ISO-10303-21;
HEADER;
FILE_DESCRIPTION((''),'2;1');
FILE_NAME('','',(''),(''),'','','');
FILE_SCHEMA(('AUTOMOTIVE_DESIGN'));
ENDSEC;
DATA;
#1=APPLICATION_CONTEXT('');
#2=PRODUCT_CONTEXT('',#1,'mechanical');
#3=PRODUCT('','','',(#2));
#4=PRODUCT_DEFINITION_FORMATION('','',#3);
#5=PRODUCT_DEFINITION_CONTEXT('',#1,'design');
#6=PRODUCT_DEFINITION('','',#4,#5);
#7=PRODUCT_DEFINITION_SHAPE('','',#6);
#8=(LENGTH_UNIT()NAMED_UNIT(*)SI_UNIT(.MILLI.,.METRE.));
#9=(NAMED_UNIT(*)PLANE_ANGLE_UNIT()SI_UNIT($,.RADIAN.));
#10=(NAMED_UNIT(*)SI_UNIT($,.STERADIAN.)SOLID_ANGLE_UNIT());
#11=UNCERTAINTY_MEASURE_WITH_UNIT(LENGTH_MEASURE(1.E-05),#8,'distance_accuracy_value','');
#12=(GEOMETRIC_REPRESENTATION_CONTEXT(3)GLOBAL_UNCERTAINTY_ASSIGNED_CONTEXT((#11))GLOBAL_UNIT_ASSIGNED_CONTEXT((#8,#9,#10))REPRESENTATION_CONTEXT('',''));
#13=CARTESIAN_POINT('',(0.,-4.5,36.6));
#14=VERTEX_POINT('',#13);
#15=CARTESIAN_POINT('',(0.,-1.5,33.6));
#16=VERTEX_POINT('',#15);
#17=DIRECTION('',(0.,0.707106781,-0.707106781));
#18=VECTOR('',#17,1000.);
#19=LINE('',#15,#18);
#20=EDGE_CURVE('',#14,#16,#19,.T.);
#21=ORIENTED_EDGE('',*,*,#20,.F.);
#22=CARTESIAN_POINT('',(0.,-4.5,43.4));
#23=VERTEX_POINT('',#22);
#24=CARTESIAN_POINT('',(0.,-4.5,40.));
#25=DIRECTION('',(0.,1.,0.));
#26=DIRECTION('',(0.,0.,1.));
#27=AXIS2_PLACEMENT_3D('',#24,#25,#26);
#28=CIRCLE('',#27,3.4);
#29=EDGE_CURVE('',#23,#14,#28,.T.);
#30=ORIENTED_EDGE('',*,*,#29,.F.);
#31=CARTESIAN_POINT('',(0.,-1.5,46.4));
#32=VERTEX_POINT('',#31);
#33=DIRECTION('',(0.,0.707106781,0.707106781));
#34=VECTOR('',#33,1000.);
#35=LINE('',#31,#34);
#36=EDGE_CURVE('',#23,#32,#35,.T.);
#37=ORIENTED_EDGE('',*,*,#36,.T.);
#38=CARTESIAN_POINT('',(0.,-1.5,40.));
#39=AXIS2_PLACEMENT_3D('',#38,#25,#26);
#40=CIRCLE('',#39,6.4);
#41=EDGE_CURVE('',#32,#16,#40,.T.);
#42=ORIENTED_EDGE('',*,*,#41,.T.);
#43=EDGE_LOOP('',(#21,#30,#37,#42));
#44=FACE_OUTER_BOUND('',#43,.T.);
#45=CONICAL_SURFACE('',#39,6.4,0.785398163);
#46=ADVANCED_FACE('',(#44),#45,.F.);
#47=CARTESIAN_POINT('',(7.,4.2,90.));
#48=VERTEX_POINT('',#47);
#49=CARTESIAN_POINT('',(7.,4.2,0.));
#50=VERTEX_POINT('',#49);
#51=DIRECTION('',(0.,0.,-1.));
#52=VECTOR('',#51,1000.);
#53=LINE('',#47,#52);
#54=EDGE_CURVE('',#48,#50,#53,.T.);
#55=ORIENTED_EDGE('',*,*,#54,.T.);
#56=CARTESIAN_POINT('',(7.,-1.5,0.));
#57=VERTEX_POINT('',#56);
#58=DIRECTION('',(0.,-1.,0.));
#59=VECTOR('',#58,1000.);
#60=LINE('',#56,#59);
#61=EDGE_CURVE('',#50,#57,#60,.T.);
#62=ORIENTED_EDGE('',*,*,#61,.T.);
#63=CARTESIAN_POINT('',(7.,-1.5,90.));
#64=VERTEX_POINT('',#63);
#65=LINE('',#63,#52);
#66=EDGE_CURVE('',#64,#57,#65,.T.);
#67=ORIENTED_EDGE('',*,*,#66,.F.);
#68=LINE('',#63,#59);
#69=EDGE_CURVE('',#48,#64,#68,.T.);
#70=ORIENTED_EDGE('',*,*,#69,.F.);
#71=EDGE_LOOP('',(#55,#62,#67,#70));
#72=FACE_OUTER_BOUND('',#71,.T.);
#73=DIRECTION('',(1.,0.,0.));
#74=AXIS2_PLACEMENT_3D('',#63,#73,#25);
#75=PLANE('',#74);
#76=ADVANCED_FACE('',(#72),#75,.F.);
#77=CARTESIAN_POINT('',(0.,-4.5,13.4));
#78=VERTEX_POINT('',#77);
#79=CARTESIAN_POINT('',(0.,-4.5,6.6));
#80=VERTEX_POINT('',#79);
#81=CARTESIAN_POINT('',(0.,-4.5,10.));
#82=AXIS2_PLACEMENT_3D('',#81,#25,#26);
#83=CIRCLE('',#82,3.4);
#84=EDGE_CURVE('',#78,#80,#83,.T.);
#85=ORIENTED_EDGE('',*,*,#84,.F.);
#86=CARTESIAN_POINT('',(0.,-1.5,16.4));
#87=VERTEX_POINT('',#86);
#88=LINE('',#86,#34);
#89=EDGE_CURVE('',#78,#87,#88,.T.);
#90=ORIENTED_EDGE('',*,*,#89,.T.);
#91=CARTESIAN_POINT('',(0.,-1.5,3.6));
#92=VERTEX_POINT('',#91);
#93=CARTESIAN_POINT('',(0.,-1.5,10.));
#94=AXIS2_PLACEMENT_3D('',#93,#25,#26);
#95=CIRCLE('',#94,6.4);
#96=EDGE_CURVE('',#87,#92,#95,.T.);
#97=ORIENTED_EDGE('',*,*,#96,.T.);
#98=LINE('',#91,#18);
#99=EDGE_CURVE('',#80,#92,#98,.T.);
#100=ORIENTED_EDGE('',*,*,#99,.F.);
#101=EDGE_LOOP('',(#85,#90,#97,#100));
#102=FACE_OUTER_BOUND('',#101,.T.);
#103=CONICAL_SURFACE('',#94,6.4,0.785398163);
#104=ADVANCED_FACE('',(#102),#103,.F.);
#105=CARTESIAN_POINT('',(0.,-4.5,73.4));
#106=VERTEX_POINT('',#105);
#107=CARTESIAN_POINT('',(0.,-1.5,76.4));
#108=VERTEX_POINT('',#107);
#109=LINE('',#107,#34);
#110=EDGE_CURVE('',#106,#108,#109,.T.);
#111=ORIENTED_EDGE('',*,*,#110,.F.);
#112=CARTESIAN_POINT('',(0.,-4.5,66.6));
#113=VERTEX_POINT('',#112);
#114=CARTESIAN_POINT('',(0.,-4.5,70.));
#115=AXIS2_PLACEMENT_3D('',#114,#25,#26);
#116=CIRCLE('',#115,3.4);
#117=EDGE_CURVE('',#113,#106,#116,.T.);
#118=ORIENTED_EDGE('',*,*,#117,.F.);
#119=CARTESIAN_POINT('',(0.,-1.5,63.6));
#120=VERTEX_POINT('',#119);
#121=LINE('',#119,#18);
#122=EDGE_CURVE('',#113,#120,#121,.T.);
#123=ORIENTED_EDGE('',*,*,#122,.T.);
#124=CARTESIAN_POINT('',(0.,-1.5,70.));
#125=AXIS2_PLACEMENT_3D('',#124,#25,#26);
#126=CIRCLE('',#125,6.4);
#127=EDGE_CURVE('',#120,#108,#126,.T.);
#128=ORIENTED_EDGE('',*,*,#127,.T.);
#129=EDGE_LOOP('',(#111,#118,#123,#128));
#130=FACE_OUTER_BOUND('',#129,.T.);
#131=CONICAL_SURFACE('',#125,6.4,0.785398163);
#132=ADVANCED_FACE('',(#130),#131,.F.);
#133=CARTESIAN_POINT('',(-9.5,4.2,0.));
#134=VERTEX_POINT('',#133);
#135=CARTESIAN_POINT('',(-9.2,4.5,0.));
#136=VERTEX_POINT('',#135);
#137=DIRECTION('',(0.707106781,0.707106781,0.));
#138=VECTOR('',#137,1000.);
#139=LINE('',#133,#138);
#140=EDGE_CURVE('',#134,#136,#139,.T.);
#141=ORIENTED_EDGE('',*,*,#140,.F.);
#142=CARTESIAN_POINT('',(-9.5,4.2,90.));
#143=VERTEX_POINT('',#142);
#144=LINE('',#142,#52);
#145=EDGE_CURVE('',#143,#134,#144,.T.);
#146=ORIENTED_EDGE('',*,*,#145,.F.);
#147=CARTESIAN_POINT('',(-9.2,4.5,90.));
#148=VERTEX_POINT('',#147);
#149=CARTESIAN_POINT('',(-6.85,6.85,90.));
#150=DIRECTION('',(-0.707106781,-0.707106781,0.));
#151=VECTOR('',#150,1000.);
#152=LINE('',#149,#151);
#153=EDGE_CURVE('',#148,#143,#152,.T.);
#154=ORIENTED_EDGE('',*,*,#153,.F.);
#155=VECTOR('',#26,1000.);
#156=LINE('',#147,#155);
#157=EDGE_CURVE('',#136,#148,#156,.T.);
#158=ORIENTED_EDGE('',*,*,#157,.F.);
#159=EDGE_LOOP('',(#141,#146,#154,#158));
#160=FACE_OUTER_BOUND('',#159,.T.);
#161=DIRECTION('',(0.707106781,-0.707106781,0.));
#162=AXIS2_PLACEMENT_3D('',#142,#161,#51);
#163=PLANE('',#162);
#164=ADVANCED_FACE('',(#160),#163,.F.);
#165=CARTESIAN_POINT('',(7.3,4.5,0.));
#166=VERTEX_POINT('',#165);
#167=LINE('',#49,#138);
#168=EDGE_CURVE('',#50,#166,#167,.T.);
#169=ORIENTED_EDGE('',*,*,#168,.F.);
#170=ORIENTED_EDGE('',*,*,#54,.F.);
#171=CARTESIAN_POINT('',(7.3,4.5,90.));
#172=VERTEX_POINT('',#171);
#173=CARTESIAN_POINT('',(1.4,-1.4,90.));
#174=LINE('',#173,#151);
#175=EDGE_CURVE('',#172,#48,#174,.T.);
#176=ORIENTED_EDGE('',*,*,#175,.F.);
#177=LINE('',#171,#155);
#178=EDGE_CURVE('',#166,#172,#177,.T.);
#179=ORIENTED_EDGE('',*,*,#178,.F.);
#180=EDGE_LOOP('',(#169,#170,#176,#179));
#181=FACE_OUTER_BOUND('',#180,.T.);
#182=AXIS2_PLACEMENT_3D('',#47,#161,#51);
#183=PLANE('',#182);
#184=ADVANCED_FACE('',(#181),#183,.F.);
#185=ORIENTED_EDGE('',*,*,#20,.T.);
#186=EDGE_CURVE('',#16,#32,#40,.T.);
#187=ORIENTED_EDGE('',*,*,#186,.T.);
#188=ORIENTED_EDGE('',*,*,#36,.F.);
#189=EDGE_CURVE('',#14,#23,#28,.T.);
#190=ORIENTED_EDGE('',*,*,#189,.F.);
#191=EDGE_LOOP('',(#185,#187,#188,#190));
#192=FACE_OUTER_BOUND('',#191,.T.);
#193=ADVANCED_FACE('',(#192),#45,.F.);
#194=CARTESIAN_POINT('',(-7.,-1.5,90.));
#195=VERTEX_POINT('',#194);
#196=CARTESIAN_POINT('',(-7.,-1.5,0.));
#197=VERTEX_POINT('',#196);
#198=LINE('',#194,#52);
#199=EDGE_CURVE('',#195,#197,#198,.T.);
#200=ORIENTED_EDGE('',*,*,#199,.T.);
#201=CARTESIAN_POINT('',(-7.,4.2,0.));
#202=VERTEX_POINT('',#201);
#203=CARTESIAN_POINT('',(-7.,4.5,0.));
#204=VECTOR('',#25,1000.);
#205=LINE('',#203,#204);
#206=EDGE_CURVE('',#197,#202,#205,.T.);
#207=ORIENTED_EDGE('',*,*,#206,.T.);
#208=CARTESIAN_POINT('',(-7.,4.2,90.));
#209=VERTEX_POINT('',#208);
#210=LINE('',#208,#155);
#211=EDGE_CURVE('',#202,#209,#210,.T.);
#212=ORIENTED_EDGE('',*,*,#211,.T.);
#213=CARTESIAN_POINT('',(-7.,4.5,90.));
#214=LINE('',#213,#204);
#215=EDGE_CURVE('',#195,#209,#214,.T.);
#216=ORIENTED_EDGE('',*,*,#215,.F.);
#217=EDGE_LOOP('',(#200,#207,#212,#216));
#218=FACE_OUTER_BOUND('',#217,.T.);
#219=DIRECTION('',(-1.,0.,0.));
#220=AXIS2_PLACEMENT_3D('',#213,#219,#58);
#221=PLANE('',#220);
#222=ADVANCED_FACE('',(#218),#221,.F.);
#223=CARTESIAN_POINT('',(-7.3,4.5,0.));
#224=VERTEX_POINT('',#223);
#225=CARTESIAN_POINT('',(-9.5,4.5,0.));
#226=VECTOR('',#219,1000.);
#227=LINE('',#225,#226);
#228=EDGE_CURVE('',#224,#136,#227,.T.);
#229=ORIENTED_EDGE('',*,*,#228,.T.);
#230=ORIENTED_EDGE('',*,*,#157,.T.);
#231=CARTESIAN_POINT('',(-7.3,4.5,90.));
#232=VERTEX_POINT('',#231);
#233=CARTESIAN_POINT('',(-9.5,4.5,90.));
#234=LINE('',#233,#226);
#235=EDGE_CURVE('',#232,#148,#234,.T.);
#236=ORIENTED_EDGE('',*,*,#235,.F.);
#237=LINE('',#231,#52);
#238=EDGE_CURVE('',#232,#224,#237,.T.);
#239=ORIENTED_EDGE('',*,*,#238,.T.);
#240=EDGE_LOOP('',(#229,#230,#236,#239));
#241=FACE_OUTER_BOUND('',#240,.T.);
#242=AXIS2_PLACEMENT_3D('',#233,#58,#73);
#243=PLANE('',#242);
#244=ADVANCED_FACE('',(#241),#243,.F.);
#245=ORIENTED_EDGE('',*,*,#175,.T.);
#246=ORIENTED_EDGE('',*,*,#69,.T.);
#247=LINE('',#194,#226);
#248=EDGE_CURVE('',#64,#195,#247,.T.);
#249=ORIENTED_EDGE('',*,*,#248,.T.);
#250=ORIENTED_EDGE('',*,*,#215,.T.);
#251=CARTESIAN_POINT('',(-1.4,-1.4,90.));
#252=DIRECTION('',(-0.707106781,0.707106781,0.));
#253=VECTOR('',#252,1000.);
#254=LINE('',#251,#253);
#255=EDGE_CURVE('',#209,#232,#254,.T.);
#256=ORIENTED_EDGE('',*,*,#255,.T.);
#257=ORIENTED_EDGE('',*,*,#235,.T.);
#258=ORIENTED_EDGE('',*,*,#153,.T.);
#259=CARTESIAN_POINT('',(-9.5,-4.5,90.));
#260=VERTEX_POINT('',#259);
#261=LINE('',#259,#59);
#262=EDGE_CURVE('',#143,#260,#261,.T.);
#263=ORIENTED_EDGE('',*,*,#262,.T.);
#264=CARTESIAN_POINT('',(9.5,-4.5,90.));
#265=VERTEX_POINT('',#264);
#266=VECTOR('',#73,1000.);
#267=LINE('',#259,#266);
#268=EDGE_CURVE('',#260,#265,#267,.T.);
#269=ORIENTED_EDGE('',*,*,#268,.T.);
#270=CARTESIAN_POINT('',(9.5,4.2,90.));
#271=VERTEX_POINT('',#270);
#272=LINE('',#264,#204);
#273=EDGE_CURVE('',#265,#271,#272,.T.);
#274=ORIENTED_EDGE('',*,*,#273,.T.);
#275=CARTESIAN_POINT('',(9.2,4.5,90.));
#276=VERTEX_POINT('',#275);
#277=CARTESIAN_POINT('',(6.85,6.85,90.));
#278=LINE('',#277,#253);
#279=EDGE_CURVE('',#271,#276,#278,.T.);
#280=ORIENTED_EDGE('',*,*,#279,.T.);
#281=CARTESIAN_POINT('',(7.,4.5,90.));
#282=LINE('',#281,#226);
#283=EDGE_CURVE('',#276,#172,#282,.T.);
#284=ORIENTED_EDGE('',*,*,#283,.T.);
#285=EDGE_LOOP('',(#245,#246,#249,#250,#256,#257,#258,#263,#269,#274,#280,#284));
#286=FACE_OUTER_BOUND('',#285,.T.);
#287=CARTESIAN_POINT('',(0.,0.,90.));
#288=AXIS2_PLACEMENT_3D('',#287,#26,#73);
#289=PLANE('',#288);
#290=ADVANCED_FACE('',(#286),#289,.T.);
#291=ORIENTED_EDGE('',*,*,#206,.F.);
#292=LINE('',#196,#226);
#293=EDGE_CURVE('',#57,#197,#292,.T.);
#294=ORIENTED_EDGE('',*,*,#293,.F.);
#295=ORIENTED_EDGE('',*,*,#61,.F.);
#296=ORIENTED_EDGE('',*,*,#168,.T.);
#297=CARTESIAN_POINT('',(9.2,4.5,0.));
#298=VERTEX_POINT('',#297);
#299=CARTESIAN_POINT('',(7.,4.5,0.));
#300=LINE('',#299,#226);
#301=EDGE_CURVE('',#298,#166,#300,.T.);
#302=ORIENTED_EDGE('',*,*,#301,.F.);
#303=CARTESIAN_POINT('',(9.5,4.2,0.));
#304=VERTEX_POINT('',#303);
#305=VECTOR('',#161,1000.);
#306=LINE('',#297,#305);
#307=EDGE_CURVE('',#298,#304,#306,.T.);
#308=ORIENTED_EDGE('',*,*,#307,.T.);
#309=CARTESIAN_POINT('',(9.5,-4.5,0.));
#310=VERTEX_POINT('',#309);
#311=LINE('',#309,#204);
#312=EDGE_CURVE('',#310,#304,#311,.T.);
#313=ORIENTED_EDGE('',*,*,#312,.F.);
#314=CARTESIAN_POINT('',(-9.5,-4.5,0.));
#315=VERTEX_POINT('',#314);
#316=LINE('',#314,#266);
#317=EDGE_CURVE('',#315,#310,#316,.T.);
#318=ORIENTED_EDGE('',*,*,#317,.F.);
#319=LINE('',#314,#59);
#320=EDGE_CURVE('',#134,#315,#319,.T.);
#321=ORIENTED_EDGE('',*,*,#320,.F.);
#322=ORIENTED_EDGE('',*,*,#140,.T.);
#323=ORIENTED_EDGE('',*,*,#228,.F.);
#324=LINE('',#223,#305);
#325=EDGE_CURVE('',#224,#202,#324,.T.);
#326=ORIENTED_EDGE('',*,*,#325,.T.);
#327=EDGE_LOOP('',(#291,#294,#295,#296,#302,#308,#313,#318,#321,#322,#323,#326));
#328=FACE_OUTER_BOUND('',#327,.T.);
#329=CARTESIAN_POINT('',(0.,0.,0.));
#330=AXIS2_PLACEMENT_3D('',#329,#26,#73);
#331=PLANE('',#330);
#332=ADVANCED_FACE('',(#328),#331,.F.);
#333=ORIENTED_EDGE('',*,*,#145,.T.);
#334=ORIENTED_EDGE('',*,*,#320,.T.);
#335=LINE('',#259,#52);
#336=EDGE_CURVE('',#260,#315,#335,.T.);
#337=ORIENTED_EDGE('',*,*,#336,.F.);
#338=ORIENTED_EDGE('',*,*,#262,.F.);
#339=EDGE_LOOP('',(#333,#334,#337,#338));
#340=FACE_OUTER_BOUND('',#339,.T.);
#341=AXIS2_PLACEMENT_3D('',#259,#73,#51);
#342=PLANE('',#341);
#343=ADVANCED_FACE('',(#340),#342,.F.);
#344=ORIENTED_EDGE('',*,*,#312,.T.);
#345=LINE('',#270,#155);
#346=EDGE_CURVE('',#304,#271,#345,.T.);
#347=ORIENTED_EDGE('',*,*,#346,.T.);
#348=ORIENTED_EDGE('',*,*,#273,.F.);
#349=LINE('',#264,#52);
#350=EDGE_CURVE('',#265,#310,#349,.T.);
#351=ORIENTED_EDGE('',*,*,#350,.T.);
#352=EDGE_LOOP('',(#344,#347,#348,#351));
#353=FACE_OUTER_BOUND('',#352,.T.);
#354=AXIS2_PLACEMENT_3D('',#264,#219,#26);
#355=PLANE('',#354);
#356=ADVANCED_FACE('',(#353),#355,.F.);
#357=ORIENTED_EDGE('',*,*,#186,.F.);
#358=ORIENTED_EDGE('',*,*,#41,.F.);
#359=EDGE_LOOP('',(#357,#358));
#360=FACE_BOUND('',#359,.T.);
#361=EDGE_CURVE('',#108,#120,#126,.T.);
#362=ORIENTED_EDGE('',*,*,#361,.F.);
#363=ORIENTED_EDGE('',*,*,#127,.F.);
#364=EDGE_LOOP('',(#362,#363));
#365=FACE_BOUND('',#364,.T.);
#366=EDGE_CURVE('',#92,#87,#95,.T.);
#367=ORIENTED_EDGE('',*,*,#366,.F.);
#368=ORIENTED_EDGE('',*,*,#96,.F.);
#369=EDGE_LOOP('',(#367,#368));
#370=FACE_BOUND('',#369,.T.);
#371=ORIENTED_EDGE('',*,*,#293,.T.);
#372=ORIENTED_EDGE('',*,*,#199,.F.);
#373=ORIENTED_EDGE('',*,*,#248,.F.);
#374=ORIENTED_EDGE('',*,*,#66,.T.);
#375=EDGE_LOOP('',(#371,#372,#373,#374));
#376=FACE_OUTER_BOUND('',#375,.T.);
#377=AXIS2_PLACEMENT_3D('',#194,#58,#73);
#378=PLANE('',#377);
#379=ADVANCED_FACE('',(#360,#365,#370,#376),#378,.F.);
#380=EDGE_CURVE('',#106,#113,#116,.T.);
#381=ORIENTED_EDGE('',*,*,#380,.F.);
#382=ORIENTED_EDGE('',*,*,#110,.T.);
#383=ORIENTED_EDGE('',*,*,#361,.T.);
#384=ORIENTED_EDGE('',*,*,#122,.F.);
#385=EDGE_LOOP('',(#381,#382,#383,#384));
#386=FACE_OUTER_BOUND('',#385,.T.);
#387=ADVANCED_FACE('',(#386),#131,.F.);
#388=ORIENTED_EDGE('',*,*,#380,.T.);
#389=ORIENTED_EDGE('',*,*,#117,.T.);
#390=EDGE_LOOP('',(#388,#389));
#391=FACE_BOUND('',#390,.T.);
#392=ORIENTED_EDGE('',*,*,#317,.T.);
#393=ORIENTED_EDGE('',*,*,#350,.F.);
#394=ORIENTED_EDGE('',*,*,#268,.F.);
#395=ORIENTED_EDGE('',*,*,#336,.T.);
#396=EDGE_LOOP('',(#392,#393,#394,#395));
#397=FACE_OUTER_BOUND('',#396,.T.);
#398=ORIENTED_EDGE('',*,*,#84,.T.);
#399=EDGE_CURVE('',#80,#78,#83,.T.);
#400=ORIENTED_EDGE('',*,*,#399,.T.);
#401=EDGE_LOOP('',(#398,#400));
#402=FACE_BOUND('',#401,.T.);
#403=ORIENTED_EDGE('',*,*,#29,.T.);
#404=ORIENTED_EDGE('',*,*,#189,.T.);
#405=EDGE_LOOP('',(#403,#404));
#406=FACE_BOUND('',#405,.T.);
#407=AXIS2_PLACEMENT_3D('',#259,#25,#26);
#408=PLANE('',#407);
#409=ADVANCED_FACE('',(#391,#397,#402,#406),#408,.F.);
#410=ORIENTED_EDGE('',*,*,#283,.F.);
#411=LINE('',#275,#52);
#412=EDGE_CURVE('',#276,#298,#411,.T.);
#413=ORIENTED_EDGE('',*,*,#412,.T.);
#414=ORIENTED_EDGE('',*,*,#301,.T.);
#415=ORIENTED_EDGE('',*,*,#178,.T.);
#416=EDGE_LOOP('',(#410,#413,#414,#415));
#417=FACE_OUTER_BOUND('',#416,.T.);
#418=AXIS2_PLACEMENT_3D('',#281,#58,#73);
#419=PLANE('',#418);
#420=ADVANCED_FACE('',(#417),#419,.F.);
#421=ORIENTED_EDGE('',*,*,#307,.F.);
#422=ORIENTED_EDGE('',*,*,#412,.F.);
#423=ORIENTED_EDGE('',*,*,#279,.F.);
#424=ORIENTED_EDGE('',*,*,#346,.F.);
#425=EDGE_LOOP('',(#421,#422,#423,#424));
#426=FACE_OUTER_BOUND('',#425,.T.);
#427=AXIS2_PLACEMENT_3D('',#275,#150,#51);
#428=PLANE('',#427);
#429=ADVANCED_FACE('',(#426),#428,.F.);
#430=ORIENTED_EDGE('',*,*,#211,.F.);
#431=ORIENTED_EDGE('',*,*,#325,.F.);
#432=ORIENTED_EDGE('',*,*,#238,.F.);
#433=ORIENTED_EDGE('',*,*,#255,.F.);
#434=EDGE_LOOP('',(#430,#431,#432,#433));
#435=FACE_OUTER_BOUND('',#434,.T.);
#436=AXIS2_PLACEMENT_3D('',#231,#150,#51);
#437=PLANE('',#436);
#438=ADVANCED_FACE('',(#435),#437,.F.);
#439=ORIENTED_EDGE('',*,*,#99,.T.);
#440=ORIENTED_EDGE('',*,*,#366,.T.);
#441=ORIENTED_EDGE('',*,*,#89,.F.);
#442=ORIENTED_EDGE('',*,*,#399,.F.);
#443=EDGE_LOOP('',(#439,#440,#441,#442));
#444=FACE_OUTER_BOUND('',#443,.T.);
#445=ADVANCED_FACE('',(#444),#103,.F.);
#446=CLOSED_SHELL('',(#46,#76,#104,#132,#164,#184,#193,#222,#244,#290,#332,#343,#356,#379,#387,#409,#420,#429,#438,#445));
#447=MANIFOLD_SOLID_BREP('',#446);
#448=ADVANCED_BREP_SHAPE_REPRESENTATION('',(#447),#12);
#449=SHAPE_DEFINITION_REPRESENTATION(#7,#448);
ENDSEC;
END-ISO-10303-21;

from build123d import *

# Parameters (mm, degrees)
BOSS_EXTRUDE1_DEPTH                         = 90
HOLE_SIZE_PER_HEX_SOCKET_LOBED_SEMI_2_COUNT = 2
HOLE_SIZE_PER_HEX_SOCKET_LOBED_SEMI_2_PITCH = 30
LPATTERN1_COUNT                             = 2
LPATTERN1_PITCH                             = 30
CHAMFER1_SIZE                               = 0.3


with BuildPart() as part:
    # Sketch1 → Boss-Extrude1 (new body)
    with BuildSketch(Plane.XY):
        Polygon((-7, 4.5), (-7, -1.5), (7, -1.5), (7, 4.5), (9.5, 4.5), (9.5, -4.5), (-9.5, -4.5), (-9.5, 4.5), align=None)
    extrude(amount=BOSS_EXTRUDE1_DEPTH)

    # Sketch5 → Hole size per hex socket lobed semi-countersunk screw type1 (revolve, cut)
    with BuildSketch(Plane(origin=(0, -1.5, 10), x_dir=(0, 0, 1), z_dir=(1, 0, 0))):
        Polygon((0, 0), (0, 3), (3.3, 3), (3.3, 3.1), (6.4, 0), align=None)
    hole_size_per_hex_socket_lobed_semi_coun = revolve(axis=Axis((0, 4.85, 10), (0, -1, 0)), mode=Mode.SUBTRACT)

    # Hole size per hex socket lobed semi- 2: Hole size per hex socket lobed semi-countersunk screw type1 ×2
    with Locations(*[(0, 0, i * HOLE_SIZE_PER_HEX_SOCKET_LOBED_SEMI_2_PITCH) for i in range(1, HOLE_SIZE_PER_HEX_SOCKET_LOBED_SEMI_2_COUNT)]):
        add(hole_size_per_hex_socket_lobed_semi_coun, mode=Mode.SUBTRACT)

    # LPattern1: Hole size per hex socket lobed semi-countersunk screw type1 ×2
    with Locations(*[(0, 0, i * LPATTERN1_PITCH) for i in range(1, LPATTERN1_COUNT)]):
        add(hole_size_per_hex_socket_lobed_semi_coun, mode=Mode.SUBTRACT)

    # LPattern1 copy 1 sketch → LPattern1 copy 1 (revolve, cut)
    with BuildSketch(Plane(origin=(0, -1.5, 70), x_dir=(0, 0, 1), z_dir=(1, 0, 0))):
        Polygon((0, 0), (0, 3), (3.3, 3), (3.3, 3.1), (6.4, 0), align=None)
    revolve(axis=Axis((0, 4.85, 70), (0, -1, 0)), mode=Mode.SUBTRACT)

    # Chamfer1
    chamfer1_edges = [part.edges().sort_by_distance(p)[0] for p in [
        (9.5, 4.5, 45),
        (-9.5, 4.5, 45),
        (-7, 4.5, 45),
        (7, 4.5, 45),
    ]]
    chamfer(chamfer1_edges, length=CHAMFER1_SIZE)


solid = part.part
